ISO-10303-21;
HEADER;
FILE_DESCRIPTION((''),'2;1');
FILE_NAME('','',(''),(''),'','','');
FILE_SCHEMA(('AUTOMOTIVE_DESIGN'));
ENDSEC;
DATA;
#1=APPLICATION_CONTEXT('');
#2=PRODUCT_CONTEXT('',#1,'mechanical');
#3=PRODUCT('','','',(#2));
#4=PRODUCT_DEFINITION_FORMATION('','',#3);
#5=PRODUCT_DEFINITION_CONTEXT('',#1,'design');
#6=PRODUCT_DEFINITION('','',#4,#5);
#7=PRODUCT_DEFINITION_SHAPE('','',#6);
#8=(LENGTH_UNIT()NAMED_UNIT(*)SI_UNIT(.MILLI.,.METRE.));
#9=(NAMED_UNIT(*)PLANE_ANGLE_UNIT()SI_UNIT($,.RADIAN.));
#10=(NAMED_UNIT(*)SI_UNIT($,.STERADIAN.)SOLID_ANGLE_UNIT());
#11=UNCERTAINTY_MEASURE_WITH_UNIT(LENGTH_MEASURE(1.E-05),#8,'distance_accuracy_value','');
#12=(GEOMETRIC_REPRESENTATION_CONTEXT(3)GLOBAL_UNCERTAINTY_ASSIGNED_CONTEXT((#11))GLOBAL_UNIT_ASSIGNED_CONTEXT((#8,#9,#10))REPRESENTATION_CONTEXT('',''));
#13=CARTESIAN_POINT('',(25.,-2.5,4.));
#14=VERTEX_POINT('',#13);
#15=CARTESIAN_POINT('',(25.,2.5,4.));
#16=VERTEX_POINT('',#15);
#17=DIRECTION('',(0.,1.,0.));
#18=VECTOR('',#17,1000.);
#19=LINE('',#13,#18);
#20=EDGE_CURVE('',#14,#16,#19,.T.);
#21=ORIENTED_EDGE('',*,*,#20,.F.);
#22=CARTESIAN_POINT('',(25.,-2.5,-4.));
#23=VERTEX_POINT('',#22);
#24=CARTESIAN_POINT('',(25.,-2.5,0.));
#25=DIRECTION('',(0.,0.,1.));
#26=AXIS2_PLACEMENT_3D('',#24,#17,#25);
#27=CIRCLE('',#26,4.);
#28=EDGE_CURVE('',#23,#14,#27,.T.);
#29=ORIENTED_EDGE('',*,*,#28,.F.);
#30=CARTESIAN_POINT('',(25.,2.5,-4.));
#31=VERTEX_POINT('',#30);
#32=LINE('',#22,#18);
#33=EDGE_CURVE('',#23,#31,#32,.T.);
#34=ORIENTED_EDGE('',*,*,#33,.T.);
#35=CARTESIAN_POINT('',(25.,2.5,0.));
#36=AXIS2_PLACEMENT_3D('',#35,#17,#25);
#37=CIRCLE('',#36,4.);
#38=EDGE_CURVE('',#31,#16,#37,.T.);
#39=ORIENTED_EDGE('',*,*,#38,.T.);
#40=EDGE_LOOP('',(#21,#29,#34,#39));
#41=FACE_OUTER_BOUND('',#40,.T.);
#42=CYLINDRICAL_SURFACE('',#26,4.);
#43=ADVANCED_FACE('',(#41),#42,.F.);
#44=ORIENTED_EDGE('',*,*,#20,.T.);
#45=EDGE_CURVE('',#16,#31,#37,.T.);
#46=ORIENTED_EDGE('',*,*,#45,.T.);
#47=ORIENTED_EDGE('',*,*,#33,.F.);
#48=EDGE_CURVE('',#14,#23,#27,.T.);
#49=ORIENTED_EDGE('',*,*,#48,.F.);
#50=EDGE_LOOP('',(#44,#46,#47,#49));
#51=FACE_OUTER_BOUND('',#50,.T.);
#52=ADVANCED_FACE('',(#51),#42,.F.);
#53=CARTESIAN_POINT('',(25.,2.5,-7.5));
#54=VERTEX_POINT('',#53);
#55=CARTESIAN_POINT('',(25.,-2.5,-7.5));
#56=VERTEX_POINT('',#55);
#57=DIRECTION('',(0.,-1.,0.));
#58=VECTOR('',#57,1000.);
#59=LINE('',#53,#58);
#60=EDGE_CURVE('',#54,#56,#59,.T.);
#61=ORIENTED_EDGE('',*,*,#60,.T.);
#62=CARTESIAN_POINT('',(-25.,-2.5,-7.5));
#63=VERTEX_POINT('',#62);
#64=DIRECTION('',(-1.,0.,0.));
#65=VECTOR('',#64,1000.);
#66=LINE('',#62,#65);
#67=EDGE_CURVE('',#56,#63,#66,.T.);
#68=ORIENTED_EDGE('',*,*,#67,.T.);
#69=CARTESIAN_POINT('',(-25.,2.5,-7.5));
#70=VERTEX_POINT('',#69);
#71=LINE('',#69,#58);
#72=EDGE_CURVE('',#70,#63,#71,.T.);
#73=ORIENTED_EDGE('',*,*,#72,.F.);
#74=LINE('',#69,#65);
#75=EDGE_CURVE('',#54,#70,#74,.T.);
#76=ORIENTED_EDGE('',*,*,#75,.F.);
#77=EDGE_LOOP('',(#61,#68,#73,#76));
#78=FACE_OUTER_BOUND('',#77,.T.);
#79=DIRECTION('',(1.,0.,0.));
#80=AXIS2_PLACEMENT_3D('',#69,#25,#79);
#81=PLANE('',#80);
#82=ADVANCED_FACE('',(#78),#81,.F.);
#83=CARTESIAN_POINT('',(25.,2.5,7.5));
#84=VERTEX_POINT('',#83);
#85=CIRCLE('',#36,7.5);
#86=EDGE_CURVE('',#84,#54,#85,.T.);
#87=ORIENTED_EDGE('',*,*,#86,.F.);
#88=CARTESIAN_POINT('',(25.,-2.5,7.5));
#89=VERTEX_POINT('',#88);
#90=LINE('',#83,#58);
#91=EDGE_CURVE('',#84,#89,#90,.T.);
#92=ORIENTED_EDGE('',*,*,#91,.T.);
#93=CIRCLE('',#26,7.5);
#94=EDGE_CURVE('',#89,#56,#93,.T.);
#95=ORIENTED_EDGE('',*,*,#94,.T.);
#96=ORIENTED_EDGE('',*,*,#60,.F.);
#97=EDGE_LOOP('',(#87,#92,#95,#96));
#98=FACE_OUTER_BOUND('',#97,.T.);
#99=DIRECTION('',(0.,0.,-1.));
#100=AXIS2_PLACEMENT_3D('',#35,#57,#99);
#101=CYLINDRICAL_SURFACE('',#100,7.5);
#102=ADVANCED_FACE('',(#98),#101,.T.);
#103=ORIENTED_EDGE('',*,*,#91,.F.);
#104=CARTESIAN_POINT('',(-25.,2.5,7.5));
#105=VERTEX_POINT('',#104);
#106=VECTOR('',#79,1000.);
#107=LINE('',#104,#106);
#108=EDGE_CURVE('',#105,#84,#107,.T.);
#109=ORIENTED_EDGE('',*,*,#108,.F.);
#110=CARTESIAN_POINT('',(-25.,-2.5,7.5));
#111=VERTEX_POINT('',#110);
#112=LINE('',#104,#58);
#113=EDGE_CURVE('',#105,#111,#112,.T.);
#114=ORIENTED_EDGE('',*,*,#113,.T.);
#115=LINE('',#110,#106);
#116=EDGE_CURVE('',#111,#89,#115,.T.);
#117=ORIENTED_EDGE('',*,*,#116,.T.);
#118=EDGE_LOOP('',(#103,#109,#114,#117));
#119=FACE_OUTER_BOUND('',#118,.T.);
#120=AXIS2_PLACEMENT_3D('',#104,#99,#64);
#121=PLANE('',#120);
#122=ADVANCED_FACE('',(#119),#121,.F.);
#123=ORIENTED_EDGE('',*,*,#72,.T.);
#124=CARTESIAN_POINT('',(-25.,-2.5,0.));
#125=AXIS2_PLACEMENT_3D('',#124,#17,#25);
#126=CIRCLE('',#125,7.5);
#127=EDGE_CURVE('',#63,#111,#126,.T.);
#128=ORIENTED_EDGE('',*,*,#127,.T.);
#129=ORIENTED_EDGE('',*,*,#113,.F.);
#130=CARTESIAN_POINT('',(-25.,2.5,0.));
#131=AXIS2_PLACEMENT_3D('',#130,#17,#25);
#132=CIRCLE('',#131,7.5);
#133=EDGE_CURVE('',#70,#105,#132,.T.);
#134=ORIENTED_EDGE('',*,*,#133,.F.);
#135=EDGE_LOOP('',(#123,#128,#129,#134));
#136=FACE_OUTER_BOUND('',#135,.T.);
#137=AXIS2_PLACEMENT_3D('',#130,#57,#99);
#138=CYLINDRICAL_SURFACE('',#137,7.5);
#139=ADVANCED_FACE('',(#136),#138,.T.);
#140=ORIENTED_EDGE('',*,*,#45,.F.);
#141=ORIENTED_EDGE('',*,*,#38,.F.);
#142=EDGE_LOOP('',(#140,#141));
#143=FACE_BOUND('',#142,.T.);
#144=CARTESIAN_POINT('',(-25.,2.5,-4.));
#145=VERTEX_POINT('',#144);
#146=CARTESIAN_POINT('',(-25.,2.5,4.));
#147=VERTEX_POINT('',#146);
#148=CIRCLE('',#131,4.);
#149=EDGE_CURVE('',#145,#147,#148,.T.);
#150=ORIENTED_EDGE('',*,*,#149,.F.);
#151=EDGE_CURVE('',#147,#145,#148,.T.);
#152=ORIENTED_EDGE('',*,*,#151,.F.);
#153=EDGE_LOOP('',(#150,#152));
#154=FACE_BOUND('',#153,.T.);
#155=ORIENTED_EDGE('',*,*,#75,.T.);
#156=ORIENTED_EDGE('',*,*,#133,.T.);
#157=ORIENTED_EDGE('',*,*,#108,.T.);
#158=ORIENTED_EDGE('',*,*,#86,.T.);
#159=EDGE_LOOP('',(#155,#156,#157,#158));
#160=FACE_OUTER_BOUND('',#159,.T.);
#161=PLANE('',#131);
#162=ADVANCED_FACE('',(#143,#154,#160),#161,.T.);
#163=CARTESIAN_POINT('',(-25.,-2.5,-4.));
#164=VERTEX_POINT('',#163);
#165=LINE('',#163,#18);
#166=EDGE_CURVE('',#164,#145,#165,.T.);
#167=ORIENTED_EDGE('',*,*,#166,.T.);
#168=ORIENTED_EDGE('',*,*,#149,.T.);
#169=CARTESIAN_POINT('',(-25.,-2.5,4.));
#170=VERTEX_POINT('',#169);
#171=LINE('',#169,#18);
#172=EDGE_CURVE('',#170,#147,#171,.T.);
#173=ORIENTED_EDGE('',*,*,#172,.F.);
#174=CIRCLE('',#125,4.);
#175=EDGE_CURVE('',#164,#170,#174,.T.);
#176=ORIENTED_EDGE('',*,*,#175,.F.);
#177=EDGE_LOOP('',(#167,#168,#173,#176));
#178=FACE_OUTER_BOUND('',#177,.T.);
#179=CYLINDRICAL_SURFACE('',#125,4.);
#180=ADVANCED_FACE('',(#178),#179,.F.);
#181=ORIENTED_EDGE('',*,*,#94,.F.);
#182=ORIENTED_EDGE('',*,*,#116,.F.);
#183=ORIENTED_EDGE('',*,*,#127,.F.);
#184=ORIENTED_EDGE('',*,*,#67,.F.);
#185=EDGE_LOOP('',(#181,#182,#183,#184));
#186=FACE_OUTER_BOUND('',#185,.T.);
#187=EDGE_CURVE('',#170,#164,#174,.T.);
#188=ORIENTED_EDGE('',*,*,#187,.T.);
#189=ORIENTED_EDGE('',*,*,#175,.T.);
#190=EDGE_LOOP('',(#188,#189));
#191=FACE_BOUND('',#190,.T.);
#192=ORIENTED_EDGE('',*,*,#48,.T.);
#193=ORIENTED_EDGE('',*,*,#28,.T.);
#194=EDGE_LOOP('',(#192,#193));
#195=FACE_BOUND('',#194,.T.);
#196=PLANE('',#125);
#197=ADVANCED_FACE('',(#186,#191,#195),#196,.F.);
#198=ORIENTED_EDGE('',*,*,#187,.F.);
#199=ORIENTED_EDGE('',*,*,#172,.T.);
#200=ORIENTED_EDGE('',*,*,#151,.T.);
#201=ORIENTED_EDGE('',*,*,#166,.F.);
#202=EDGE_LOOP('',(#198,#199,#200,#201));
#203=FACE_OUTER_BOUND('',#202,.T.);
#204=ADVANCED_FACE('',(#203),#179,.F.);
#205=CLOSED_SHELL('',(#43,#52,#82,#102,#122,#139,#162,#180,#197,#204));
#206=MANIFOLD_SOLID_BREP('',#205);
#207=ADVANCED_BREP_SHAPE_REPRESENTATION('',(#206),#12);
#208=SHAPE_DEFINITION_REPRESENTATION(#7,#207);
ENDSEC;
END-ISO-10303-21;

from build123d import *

# Parameters (mm, degrees)
LINK_PLATE_DEPTH     = 2.5
PIN_HOLES_SKETCH_R   = 4
PIN_HOLES_2X_8_DEPTH = 2.5


with BuildPart() as part:
    # Link Profile Sketch → Link Plate (new, symmetric)
    with BuildSketch(Plane(origin=(0, 0, 0), x_dir=(1, 0, 0), z_dir=(0, 1, 0))):
        with BuildLine():
            Line((-25, 7.5), (25, 7.5))
            ThreePointArc((25, 7.5), (32.5, 0), (25, -7.5))
            Line((25, -7.5), (-25, -7.5))
            ThreePointArc((-25, -7.5), (-32.5, 0), (-25, 7.5))
        make_face()
    extrude(amount=LINK_PLATE_DEPTH, both=True)

    # Pin Holes Sketch → Pin Holes 2xØ8 (cut, symmetric)
    with BuildSketch(Plane(origin=(0, 0, 0), x_dir=(1, 0, 0), z_dir=(0, 1, 0))):
        with Locations(Location((-25, 0, 0), (0, 0, 270))):
            Circle(PIN_HOLES_SKETCH_R)
        with Locations(Location((25, 0, 0), (0, 0, 270))):
            Circle(PIN_HOLES_SKETCH_R)
    extrude(amount=PIN_HOLES_2X_8_DEPTH, both=True, mode=Mode.SUBTRACT)


solid = part.part
